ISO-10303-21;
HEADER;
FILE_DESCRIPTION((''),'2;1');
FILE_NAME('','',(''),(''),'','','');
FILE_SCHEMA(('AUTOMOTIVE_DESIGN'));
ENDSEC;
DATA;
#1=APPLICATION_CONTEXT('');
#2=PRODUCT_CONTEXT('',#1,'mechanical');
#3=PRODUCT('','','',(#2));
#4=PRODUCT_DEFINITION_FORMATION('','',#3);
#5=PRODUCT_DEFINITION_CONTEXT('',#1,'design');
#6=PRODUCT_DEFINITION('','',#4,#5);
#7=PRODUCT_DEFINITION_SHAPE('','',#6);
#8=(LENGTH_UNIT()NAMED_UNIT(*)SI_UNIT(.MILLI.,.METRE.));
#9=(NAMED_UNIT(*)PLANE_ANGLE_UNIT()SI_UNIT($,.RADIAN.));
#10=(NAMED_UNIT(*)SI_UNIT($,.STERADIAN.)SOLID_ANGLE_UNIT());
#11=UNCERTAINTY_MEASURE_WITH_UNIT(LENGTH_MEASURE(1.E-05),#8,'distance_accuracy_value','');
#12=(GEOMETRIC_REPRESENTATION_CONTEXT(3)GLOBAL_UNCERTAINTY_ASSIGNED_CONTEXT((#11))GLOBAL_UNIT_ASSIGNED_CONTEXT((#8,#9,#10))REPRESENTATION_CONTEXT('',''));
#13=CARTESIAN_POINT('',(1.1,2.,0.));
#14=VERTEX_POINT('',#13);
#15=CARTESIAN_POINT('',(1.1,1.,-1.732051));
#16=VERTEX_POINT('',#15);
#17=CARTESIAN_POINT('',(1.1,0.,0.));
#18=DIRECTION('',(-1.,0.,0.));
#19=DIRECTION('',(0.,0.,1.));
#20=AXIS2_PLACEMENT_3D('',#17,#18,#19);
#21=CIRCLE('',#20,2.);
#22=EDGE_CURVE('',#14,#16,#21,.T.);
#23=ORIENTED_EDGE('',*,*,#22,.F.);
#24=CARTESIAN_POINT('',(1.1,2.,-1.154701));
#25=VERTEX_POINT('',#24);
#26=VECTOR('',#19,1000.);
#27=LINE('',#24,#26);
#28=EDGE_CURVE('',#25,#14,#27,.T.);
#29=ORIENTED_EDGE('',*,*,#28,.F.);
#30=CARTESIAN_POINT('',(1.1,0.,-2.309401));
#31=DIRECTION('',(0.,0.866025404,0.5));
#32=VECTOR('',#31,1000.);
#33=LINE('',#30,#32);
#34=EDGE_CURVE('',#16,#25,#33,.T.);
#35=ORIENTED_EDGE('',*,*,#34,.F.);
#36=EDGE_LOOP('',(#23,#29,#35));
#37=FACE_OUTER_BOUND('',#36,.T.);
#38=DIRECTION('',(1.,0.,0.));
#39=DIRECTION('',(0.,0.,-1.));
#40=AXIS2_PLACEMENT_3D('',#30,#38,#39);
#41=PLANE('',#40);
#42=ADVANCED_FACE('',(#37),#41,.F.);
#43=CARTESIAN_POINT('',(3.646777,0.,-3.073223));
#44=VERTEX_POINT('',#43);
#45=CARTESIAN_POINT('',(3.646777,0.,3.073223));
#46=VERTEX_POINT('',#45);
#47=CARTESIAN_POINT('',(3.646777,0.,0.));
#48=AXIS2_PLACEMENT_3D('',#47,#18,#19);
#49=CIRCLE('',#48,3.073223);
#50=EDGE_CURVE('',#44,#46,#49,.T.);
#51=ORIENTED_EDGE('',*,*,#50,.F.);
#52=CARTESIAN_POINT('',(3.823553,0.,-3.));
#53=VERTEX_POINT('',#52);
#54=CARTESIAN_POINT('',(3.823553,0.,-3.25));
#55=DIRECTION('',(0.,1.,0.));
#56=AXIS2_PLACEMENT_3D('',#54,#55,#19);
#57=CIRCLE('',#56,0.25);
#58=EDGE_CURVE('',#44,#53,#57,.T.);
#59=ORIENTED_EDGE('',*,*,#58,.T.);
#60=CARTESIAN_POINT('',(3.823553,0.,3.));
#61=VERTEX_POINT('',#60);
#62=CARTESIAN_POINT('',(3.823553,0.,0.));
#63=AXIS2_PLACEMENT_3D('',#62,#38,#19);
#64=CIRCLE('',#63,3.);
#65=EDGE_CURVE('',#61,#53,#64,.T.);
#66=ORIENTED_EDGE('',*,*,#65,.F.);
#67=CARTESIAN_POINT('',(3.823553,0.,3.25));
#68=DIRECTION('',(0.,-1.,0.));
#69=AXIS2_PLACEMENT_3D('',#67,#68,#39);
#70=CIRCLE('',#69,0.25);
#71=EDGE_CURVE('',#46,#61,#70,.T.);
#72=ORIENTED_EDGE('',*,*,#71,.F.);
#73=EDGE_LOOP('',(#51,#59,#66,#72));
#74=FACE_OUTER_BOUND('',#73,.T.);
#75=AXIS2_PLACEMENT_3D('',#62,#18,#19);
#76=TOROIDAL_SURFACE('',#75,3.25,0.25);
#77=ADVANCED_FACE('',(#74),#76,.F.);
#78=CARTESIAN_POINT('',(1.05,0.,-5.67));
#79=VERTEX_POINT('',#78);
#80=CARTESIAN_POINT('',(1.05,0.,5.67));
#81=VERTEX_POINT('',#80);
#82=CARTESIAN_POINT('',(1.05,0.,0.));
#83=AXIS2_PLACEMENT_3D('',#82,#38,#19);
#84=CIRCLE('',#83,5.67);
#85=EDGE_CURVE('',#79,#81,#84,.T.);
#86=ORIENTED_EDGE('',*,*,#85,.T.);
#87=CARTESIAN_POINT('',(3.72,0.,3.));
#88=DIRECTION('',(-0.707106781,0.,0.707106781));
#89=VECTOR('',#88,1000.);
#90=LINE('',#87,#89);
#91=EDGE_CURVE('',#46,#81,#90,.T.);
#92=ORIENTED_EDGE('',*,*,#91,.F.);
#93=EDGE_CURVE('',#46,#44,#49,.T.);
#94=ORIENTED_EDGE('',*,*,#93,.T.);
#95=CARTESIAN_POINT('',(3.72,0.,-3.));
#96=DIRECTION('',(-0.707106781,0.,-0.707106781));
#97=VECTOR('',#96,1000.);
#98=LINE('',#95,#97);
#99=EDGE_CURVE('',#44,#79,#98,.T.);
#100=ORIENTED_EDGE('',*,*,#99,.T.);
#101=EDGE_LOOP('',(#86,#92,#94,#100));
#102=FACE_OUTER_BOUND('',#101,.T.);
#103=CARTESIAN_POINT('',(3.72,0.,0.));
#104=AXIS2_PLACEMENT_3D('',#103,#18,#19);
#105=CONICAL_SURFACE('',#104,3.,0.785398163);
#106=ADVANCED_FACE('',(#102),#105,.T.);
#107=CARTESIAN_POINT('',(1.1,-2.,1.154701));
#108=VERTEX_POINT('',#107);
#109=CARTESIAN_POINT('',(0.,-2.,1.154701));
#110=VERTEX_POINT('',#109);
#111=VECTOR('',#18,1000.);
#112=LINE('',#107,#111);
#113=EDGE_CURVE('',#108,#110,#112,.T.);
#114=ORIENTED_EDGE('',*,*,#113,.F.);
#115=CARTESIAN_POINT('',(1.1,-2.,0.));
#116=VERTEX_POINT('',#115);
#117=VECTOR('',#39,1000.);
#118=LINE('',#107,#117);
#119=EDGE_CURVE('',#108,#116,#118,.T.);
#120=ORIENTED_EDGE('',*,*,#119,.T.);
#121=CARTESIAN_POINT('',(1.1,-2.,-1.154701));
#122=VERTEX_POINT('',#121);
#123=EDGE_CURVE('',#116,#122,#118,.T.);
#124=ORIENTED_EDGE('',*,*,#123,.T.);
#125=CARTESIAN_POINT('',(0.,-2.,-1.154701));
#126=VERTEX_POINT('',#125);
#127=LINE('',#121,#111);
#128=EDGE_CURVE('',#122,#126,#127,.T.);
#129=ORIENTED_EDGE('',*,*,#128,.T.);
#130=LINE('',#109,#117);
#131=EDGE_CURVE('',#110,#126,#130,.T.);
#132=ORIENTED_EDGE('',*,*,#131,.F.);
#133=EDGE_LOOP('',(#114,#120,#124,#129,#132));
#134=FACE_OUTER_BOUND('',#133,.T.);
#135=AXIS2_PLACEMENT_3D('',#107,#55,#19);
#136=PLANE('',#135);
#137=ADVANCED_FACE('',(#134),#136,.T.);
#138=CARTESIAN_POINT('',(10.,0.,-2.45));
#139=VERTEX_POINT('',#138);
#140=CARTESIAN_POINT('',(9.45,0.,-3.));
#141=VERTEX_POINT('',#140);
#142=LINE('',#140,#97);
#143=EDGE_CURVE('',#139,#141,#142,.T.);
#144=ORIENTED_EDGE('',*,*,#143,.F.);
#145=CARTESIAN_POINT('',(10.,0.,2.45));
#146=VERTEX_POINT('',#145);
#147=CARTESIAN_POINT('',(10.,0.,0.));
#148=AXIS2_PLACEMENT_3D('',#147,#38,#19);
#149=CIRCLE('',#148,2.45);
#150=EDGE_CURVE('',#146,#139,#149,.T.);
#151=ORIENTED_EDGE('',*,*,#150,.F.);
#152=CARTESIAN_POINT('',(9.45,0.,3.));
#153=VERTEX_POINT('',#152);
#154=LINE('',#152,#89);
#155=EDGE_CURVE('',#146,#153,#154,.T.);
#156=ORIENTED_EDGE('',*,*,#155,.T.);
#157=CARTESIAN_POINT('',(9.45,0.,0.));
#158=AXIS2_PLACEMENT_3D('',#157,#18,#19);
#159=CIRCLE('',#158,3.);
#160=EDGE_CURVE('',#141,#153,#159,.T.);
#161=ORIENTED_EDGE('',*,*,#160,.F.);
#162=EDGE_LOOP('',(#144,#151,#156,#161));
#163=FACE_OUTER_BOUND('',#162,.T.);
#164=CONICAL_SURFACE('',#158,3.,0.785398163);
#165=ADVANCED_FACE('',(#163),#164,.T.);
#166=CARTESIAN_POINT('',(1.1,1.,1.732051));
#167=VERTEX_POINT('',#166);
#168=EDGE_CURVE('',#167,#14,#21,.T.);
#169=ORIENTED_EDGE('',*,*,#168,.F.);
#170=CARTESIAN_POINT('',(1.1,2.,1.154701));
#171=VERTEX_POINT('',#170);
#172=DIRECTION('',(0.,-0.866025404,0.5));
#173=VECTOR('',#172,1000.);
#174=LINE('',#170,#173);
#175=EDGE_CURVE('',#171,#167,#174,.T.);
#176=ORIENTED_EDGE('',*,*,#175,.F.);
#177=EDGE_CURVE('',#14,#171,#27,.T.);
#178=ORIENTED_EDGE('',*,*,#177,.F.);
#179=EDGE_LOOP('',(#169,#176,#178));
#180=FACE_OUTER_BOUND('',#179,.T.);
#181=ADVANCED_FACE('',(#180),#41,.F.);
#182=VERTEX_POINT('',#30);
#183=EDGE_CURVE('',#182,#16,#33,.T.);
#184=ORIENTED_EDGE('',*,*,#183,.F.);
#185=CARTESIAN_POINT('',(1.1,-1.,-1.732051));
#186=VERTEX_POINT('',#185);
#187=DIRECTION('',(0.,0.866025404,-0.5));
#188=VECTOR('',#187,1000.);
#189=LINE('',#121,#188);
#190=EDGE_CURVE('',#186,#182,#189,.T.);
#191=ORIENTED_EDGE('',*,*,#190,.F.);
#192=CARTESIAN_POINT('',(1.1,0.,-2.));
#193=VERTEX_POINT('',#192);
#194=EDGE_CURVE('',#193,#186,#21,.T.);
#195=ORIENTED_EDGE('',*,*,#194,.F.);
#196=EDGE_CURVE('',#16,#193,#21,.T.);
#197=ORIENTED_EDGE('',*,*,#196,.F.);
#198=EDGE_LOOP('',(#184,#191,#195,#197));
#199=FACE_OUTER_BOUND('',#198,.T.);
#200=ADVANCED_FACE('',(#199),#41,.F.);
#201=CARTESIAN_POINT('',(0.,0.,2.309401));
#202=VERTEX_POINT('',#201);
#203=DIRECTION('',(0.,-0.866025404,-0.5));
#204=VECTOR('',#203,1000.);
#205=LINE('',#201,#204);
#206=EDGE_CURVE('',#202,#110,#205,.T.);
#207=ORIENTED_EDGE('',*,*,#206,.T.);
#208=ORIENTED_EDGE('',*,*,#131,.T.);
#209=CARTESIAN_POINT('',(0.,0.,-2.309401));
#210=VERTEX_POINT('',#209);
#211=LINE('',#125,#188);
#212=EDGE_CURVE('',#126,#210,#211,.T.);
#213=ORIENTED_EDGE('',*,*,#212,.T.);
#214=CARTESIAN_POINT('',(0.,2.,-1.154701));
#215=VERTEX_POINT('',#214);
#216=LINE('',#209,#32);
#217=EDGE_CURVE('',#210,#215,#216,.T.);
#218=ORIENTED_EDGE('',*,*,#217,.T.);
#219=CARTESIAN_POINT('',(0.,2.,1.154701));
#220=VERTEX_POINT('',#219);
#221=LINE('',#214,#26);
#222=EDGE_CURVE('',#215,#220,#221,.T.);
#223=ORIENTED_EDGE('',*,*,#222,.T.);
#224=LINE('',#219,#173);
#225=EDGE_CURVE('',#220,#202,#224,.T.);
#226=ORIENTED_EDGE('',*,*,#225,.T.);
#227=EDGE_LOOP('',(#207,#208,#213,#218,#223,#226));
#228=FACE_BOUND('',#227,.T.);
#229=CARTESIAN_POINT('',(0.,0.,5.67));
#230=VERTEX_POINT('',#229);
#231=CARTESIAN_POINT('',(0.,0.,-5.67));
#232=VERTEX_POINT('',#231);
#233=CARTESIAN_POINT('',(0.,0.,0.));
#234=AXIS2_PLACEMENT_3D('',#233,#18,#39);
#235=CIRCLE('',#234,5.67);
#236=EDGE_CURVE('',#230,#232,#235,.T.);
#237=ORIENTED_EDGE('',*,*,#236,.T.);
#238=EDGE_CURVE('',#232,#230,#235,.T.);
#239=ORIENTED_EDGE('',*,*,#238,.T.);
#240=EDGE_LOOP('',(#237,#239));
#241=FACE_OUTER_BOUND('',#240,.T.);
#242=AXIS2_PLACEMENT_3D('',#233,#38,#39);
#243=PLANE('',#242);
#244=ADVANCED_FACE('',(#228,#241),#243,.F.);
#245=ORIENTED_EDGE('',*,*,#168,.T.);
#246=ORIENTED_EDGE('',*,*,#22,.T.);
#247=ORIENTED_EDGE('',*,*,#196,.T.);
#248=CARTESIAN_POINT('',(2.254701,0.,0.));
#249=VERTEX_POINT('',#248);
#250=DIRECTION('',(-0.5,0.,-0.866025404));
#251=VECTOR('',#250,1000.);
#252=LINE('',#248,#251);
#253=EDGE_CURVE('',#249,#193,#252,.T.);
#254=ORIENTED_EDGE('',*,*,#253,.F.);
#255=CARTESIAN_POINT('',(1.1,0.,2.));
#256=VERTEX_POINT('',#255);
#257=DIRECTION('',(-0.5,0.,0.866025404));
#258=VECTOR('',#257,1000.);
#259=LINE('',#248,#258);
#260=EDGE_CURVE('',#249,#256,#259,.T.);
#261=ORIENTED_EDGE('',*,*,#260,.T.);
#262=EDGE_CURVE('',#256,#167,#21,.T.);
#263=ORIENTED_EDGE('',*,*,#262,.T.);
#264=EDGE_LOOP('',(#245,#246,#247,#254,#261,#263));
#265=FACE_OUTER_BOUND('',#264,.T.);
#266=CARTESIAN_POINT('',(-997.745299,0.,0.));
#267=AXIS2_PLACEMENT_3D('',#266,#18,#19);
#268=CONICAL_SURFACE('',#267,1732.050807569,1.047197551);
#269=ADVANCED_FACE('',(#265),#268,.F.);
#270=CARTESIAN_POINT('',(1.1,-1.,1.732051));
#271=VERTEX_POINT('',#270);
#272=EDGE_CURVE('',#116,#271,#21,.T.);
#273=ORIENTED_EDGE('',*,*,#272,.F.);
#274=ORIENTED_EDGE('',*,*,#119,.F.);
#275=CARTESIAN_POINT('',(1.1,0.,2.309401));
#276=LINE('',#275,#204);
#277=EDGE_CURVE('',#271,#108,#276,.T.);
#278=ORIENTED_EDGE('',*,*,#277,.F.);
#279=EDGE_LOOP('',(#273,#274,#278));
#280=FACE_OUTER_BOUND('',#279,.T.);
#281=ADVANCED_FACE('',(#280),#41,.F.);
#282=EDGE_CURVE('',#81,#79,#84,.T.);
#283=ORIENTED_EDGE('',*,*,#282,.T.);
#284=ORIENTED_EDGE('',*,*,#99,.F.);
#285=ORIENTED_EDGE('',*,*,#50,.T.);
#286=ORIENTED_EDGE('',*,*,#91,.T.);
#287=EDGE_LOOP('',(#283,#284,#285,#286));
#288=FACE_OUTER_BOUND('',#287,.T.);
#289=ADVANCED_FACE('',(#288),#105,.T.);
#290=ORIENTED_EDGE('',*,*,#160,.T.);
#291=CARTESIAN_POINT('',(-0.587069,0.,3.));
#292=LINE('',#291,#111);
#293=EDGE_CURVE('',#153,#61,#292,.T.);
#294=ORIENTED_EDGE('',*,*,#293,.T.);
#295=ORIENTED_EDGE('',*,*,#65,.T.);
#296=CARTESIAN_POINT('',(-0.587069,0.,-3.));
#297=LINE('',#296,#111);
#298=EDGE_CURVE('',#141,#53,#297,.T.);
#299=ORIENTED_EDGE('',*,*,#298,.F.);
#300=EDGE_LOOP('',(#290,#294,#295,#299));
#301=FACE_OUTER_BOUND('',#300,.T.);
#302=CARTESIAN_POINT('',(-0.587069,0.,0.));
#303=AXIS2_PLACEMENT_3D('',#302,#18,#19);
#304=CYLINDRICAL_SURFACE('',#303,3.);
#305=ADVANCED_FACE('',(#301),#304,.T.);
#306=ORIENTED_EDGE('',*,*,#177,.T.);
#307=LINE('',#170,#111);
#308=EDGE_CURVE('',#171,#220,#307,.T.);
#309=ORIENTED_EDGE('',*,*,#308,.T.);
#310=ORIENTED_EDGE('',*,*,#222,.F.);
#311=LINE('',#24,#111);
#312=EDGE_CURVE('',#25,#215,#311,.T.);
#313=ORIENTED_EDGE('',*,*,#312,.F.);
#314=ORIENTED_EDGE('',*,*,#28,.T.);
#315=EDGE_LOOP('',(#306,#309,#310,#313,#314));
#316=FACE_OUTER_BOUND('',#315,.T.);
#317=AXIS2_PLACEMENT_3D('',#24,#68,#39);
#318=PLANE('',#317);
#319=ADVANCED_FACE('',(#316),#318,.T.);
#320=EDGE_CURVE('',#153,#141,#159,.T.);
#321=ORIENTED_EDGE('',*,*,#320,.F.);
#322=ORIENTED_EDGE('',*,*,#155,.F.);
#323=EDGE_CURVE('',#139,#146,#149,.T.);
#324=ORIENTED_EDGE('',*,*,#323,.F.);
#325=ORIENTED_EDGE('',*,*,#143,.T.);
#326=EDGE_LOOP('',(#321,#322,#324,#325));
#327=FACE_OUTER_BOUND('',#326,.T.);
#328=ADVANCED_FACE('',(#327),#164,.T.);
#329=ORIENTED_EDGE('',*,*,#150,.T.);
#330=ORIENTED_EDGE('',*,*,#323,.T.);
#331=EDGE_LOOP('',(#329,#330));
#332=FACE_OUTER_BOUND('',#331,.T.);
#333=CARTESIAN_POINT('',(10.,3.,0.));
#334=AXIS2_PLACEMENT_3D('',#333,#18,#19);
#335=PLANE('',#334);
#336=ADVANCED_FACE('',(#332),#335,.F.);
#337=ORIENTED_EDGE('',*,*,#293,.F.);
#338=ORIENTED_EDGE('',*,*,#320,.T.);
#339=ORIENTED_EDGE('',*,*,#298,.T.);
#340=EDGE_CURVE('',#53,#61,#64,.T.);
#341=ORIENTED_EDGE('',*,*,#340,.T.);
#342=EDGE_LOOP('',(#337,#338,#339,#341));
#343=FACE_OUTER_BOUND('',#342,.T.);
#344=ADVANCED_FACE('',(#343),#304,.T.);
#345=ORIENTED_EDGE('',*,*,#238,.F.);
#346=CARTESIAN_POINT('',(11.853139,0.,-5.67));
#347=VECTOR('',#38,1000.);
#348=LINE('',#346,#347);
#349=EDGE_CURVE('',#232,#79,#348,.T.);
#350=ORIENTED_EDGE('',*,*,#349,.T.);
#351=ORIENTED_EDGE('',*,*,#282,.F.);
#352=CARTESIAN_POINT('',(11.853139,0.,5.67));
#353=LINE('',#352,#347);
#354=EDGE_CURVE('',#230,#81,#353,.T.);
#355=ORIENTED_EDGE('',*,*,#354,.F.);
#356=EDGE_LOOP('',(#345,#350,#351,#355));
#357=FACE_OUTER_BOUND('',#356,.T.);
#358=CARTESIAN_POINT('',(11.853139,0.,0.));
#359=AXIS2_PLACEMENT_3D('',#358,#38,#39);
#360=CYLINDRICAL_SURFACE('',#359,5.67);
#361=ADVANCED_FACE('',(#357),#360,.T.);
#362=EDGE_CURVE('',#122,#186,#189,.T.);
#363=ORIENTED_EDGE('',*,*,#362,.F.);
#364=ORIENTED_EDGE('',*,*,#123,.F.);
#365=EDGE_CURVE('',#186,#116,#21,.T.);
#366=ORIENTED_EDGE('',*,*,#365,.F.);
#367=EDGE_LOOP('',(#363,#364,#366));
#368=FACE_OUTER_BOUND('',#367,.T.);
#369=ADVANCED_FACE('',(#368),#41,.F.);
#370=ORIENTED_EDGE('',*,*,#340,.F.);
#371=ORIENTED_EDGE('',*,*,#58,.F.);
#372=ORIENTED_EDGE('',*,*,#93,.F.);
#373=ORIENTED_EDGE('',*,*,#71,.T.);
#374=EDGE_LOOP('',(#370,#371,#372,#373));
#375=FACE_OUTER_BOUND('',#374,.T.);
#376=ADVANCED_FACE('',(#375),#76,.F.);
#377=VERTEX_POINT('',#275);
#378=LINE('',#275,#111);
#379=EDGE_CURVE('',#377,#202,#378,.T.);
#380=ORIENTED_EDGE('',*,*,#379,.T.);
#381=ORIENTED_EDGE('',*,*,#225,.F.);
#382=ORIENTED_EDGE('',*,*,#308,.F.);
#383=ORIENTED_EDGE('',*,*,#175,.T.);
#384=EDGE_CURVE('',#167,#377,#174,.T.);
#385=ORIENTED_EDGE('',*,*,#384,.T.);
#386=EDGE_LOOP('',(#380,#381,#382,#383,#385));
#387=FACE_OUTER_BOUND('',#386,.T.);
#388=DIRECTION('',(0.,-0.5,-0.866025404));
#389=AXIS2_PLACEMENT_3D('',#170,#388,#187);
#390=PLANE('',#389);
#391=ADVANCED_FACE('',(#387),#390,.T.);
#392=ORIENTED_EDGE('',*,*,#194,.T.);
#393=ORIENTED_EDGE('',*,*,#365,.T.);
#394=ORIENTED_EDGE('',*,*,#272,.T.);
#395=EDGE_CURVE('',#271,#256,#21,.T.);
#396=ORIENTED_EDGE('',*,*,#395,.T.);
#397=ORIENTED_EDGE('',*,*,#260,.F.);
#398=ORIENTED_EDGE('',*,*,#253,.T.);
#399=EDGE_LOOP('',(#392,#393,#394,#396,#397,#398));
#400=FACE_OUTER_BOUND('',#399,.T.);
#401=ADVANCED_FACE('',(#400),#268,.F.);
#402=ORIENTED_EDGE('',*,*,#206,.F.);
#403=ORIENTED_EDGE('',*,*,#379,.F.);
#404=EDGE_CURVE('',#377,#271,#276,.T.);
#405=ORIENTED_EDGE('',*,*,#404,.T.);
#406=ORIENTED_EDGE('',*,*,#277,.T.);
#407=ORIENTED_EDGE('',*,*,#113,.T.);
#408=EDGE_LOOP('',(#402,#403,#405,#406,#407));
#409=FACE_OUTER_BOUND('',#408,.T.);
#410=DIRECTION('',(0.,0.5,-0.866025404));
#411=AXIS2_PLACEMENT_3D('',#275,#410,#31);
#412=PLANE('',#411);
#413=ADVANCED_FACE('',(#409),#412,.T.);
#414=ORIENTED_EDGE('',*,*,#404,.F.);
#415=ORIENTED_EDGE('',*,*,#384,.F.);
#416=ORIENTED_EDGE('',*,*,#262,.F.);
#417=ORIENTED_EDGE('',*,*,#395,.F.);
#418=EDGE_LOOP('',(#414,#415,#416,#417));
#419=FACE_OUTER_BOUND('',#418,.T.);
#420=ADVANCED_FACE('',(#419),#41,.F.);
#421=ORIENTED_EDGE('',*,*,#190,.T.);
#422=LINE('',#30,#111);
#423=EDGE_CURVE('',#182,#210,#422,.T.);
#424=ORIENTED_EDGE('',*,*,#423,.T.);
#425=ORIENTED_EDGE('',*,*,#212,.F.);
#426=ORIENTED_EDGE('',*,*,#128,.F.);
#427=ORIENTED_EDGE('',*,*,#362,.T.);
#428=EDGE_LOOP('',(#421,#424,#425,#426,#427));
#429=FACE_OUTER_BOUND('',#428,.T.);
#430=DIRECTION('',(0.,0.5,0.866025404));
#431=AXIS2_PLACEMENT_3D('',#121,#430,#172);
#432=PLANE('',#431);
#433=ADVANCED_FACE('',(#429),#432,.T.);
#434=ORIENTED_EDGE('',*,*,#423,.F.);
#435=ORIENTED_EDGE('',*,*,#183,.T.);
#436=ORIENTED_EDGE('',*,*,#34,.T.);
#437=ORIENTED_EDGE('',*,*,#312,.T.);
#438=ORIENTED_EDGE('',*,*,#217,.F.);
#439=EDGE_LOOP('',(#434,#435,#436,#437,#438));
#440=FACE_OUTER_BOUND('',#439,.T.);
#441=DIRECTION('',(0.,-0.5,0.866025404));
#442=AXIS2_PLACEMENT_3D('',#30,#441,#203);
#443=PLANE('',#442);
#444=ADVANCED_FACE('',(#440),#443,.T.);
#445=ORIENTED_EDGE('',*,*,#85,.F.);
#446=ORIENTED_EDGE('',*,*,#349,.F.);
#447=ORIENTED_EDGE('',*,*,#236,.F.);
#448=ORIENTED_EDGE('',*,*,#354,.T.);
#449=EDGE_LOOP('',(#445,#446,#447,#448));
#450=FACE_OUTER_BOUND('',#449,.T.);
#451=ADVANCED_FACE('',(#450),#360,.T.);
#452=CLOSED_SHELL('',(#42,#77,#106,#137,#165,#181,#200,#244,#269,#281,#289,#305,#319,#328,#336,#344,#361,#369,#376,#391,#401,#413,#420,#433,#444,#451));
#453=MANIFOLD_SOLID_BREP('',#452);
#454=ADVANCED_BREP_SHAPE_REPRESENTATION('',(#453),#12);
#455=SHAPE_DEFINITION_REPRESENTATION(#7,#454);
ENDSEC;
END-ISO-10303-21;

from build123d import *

# Parameters (mm, degrees)
HEXAGONSOCKET_DEPTH = 1.1
HEADFILLET_R        = 0.25
CHAMFER_2_SIZE      = 0.55
SKETCH4_W           = 5
SKETCH4_H           = 5


with BuildPart() as part:
    # Sketch1 → Base (revolve)
    with BuildSketch(Plane.XY, mode=Mode.PRIVATE) as base_sk:
        Polygon((0, 0), (0, 6.72), (3.72, 3), (10, 3), (10, 0), align=None)
    revolve(base_sk.sketch.rotate(Axis((-0.587069181, 0, 0), (1, 0, 0)), 90), axis=Axis((-0.587069181, 0, 0), (1, 0, 0)))

    # Sketch2 → HexagonSocket (cut)
    with BuildSketch(Plane(origin=(0, 0, 0), x_dir=(0, 0, -1), z_dir=(1, 0, 0))):
        Polygon((2.309401077, 0), (1.154700538, 2), (-1.154700538, 2), (-2.309401077, 0), (-1.154700538, -2), (1.154700538, -2), align=None)
    extrude(amount=HEXAGONSOCKET_DEPTH, mode=Mode.SUBTRACT)

    # Sketch3 → Cut-Revolve1 (revolve, cut)
    with BuildSketch(Plane.XY, mode=Mode.PRIVATE) as cut_revolve1_sk:
        Polygon((1.1, 2), (2.254700538, 0), (1.1, 0), align=None)
    revolve(cut_revolve1_sk.sketch.rotate(Axis((-0.439109555, 0, 0), (1, 0, 0)), 90), axis=Axis((-0.439109555, 0, 0), (1, 0, 0)), mode=Mode.SUBTRACT)

    # HeadFillet
    headfillet_edges = [part.edges().sort_by_distance(p)[0] for p in [
        (3.72, 0, -3),
    ]]
    fillet(headfillet_edges, radius=HEADFILLET_R)

    # Chamfer 2
    chamfer_2_edges = [part.edges().sort_by_distance(p)[0] for p in [
        (10, 0, -3),
    ]]
    chamfer(chamfer_2_edges, length=CHAMFER_2_SIZE)

    # Sketch4 → Cut-Revolve2 (revolve, cut)
    with BuildSketch(Plane(origin=(0, 0, 0), x_dir=(1, 0, 0), z_dir=(0, 1, 0)), mode=Mode.PRIVATE) as cut_revolve2_sk:
        with Locations((0.5, 8.17)):
            Rectangle(SKETCH4_W, SKETCH4_H)
    revolve(cut_revolve2_sk.sketch.rotate(Axis((11.853138686, 0, 0), (-1, 0, 0)), 180), axis=Axis((11.853138686, 0, 0), (-1, 0, 0)), mode=Mode.SUBTRACT)


solid = part.part
